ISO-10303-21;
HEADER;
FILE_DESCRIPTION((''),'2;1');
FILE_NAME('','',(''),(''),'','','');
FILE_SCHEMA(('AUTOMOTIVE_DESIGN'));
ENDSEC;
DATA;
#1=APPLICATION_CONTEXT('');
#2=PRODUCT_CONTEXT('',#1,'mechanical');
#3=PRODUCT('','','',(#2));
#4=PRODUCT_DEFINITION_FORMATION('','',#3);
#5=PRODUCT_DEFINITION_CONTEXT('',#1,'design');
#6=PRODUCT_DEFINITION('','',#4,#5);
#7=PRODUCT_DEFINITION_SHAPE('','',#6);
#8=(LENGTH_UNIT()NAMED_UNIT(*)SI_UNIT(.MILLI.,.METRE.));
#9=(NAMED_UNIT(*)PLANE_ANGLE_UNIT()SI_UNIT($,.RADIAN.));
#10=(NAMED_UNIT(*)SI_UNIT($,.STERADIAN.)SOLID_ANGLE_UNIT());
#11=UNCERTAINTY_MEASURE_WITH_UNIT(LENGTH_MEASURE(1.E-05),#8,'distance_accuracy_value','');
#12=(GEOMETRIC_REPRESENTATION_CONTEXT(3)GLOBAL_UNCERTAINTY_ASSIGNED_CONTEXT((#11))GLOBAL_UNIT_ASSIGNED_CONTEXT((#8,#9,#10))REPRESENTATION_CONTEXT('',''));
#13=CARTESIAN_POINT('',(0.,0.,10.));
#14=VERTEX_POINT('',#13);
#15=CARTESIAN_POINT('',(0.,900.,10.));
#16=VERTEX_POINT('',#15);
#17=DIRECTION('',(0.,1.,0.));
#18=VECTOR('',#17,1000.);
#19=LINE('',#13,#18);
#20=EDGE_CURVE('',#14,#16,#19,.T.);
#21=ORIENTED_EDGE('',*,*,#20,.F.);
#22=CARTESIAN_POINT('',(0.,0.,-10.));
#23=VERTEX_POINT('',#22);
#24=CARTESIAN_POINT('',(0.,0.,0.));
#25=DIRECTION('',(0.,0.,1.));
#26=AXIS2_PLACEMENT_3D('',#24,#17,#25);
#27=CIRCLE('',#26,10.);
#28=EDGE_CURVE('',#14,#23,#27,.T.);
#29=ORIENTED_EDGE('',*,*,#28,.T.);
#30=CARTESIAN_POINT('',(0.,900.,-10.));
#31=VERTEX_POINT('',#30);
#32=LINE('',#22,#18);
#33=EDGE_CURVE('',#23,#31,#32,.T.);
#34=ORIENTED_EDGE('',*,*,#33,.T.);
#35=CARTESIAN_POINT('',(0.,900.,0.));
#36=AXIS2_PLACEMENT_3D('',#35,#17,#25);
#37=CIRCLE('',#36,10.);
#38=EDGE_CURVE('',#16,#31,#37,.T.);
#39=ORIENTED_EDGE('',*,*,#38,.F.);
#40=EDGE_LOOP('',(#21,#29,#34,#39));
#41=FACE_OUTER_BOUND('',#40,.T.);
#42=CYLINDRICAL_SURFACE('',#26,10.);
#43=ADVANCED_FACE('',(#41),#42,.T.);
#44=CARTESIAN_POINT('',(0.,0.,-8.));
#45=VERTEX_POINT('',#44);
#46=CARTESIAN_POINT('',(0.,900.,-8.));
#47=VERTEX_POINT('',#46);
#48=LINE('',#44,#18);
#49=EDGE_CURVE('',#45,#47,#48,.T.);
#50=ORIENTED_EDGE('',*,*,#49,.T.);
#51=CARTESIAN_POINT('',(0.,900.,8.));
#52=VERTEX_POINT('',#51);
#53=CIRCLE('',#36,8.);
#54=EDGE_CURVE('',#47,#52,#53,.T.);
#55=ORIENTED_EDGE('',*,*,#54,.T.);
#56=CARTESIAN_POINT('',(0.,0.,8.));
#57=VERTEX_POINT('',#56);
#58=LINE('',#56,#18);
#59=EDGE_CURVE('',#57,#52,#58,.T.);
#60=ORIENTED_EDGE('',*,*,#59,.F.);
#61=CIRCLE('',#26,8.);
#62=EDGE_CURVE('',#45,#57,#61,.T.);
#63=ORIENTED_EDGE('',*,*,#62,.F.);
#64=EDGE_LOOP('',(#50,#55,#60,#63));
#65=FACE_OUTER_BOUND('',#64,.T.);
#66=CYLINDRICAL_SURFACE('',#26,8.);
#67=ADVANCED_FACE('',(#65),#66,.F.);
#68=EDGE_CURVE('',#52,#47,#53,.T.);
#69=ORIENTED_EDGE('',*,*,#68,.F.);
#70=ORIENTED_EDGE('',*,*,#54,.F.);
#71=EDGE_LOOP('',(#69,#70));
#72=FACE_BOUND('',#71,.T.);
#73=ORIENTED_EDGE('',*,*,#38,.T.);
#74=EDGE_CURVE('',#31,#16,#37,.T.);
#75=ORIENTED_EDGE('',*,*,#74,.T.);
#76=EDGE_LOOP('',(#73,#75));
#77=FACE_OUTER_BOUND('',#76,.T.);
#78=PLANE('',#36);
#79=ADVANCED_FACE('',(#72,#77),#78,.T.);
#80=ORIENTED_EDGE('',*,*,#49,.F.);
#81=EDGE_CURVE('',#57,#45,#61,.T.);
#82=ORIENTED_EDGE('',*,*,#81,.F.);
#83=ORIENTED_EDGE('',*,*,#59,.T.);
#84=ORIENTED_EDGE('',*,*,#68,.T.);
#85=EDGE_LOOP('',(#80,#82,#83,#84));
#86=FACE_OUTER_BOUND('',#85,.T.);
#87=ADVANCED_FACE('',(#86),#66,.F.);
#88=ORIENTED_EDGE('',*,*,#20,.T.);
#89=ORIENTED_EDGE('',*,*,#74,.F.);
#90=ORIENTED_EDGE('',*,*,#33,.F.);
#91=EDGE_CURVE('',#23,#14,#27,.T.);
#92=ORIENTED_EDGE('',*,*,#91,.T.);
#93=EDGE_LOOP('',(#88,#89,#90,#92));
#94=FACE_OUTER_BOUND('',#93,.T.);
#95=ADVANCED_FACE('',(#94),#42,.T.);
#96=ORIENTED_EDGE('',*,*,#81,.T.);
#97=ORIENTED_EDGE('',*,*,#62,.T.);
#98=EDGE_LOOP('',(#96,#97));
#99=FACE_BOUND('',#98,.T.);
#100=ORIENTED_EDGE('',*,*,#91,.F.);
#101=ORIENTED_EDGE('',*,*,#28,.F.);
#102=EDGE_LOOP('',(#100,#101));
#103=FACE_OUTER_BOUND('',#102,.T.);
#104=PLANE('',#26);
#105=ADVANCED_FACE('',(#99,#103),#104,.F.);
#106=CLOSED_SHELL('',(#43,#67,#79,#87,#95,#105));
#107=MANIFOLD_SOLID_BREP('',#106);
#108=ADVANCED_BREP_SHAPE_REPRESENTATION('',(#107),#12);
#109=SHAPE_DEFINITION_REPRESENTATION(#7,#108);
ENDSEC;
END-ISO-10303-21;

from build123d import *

# Parameters (mm, degrees)
SWEEP_THIN1_PROFILE_R   = 10
SWEEP_THIN1_PROFILE_R_2 = 8


with BuildPart() as part:
    # Sweep-Thin1: sweep along a path in Sketch1
    with BuildLine(Plane.XY) as sweep_thin1_path:
        Line((0, 0), (0, 900))
    # Sweep-Thin1 profile (on start of the path) → Sweep-Thin1 (sweep)
    with BuildSketch(Plane.ZX):
        Circle(SWEEP_THIN1_PROFILE_R)
        Circle(SWEEP_THIN1_PROFILE_R_2, mode=Mode.SUBTRACT)
    sweep(path=sweep_thin1_path.line)


solid = part.part
